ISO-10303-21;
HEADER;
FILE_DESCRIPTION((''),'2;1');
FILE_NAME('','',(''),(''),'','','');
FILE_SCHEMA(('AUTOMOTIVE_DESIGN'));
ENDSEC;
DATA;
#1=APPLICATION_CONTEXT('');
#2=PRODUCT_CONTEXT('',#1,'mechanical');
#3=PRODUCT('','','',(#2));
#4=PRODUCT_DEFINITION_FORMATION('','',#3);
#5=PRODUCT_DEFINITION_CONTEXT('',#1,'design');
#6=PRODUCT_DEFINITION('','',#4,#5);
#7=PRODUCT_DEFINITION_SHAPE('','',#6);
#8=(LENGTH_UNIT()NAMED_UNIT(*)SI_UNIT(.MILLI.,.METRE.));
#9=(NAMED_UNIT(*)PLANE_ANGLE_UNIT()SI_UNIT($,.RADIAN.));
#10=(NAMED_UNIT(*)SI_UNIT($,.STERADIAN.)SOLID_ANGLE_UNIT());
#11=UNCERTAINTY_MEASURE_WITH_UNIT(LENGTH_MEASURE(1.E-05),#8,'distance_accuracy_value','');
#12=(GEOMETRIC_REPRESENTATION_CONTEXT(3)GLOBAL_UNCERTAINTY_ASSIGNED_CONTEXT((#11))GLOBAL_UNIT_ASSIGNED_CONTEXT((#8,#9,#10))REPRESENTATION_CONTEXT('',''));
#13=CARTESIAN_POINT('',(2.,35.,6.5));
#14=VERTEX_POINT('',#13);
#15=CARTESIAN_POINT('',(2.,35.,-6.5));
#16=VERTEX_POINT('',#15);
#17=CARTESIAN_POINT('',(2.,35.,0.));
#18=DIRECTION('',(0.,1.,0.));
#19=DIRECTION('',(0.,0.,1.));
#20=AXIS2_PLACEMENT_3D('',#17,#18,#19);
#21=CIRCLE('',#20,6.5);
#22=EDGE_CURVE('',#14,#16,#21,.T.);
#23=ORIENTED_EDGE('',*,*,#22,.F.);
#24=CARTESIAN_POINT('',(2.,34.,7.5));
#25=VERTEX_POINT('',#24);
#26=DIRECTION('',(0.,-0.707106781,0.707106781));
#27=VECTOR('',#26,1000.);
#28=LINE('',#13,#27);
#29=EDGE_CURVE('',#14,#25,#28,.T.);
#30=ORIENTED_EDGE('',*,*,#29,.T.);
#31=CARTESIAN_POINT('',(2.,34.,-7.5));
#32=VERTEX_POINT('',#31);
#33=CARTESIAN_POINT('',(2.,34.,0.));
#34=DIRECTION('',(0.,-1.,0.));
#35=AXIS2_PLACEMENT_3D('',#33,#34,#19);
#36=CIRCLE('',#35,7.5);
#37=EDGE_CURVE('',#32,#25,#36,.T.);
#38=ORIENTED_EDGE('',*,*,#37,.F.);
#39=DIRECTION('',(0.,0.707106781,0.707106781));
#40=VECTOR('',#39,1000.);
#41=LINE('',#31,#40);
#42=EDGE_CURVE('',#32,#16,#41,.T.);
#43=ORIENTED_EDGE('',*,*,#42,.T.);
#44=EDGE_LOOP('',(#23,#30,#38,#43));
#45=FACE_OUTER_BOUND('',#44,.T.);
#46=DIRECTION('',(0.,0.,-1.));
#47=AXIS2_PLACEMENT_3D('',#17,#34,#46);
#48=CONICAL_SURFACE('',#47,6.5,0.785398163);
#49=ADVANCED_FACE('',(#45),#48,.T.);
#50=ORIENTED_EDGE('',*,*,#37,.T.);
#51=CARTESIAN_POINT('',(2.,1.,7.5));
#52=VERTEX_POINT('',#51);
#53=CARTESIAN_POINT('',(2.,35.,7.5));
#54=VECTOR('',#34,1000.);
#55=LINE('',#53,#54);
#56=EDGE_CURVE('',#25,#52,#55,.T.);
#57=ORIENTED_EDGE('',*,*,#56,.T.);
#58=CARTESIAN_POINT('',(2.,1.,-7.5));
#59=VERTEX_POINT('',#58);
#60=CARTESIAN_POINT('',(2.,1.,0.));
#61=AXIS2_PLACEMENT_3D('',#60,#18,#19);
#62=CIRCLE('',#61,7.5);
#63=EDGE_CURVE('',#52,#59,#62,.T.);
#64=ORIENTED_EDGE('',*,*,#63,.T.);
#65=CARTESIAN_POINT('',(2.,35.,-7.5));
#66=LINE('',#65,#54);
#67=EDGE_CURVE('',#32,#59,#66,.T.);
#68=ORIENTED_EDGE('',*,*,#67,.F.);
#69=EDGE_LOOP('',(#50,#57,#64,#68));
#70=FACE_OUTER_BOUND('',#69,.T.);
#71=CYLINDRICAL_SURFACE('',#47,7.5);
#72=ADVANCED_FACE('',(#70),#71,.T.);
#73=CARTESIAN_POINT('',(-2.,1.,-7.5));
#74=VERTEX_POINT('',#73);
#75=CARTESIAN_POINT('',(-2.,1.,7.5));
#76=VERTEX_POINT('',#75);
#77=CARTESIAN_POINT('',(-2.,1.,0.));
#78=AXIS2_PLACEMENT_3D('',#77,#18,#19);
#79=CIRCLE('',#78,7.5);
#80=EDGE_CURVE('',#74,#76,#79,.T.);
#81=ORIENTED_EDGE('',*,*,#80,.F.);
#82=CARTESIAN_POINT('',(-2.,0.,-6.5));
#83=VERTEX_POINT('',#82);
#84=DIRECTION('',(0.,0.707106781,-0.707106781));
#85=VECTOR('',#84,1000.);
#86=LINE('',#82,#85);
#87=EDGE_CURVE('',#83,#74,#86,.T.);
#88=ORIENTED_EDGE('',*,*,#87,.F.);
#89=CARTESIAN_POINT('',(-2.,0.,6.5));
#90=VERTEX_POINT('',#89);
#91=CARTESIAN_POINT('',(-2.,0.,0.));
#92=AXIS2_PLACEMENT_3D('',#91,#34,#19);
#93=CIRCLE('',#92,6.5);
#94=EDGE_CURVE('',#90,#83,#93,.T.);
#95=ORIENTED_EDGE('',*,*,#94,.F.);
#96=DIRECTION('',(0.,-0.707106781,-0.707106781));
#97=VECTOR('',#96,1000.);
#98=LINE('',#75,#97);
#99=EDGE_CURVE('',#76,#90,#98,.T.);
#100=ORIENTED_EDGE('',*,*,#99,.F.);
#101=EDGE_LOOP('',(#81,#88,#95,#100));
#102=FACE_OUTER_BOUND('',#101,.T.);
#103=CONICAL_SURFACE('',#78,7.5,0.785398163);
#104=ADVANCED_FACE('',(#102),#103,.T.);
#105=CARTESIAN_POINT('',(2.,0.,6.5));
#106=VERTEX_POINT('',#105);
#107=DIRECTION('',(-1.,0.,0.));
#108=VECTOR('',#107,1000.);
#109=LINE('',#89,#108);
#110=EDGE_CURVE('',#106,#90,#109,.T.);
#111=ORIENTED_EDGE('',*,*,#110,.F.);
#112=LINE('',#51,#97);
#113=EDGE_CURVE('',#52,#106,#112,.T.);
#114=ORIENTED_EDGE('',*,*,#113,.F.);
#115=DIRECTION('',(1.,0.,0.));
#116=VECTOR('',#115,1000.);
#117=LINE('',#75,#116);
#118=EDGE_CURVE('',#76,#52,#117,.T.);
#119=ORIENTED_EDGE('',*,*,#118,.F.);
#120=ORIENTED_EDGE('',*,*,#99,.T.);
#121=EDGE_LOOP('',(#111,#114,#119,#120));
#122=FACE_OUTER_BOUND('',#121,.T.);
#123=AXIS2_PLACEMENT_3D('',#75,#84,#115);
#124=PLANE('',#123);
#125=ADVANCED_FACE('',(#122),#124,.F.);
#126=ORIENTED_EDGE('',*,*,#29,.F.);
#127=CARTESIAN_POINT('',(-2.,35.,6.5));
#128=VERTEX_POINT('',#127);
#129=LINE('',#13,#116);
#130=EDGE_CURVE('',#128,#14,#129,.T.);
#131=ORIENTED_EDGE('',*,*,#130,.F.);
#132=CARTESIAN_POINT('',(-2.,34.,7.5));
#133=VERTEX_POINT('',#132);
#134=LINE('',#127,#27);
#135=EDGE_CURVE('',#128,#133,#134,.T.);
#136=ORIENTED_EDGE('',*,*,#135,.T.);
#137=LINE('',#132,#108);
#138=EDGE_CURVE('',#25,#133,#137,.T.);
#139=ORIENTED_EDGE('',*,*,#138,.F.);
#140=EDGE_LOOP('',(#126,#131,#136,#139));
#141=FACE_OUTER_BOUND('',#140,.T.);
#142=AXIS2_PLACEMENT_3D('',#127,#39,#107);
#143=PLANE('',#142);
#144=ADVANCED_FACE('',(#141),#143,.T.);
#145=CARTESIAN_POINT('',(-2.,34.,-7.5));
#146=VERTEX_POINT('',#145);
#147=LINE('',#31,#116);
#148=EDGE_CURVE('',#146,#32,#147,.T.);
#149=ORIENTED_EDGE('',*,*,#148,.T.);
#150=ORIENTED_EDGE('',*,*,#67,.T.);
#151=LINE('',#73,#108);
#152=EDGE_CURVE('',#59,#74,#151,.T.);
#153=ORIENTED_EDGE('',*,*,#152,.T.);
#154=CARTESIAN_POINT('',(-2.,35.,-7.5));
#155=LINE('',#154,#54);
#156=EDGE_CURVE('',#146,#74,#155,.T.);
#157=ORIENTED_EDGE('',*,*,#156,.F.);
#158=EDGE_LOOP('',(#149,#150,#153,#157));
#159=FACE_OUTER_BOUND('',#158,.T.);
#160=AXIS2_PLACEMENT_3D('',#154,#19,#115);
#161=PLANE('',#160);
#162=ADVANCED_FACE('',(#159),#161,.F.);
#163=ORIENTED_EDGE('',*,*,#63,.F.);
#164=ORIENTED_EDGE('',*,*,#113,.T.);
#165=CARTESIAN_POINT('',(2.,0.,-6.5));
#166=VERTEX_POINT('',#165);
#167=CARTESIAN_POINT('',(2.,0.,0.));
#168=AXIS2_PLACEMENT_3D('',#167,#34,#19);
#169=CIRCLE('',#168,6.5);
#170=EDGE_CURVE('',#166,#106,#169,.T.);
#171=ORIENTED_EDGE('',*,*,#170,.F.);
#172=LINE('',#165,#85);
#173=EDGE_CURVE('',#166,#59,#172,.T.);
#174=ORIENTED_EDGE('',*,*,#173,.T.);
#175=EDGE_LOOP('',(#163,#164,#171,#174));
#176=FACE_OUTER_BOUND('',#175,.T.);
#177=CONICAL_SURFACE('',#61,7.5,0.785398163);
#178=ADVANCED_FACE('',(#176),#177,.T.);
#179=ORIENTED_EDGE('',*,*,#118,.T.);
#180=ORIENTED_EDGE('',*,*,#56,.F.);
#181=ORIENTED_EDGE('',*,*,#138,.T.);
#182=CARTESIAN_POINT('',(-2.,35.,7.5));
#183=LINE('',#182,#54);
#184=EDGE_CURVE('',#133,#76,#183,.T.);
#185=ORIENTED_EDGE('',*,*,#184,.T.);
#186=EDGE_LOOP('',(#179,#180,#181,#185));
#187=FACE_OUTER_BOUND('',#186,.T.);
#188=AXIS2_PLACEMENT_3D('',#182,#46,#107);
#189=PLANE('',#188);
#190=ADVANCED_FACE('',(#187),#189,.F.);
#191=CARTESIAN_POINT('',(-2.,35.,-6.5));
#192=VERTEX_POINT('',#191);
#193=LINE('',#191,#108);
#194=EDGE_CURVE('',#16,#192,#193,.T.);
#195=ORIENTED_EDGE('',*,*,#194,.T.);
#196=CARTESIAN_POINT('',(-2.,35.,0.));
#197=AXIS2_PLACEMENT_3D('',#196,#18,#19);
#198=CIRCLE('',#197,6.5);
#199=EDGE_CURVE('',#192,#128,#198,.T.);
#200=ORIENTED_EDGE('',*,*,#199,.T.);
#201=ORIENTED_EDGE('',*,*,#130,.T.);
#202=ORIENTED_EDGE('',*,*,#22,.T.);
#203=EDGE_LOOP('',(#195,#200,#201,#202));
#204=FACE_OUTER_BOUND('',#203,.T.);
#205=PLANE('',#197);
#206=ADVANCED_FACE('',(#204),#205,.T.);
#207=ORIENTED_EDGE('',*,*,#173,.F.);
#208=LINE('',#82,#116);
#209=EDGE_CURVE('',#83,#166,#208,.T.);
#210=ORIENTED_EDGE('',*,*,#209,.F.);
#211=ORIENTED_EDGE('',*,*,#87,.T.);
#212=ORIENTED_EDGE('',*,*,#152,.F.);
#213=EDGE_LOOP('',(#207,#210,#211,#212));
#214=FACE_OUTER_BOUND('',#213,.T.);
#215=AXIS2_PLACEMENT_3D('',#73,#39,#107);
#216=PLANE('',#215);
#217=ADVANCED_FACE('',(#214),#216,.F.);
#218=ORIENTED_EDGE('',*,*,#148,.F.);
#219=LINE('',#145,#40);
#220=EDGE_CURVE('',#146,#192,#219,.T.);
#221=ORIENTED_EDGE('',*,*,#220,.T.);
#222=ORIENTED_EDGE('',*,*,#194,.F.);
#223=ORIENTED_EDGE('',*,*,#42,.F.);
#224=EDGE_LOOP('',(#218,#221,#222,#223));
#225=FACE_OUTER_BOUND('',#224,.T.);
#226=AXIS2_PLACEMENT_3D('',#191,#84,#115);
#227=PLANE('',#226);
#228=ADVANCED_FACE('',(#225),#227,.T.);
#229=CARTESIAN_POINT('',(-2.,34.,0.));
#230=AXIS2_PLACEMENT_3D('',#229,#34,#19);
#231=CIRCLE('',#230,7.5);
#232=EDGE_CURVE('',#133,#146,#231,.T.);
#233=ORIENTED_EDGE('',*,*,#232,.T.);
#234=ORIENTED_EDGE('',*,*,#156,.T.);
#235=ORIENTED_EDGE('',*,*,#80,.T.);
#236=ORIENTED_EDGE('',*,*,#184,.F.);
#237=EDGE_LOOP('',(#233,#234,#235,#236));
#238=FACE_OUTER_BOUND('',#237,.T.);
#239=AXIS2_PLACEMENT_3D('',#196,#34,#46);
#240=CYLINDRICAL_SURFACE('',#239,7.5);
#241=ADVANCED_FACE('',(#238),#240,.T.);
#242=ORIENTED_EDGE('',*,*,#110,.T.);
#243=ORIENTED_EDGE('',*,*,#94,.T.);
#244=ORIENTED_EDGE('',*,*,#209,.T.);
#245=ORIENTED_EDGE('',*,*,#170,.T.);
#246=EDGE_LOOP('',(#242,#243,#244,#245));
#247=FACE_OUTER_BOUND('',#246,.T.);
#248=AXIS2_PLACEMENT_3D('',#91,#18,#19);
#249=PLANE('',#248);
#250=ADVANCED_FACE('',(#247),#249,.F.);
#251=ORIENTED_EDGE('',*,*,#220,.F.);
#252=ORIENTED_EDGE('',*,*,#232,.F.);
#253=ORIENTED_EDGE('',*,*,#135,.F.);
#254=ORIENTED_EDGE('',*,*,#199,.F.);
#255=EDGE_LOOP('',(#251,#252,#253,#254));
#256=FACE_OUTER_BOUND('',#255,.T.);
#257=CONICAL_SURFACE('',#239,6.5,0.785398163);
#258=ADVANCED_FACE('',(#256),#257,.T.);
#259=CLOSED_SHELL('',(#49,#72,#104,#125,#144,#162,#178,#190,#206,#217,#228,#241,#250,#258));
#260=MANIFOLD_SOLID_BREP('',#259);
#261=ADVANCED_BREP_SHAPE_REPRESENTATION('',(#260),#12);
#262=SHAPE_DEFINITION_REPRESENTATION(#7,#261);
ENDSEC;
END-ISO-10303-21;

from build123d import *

# Parameters (mm, degrees)
BOSS_EXTRUDE1_DEPTH = 35
CHAMFER1_SIZE       = 1


with BuildPart() as part:
    # Sketch1 → Boss-Extrude1 (new body)
    with BuildSketch(Plane(origin=(0, 0, 0), x_dir=(1, 0, 0), z_dir=(0, 1, 0))):
        with BuildLine():
            Line((-2, 7.5), (2, 7.5))
            ThreePointArc((2, 7.5), (9.5, 0), (2, -7.5))
            Line((2, -7.5), (-2, -7.5))
            ThreePointArc((-2, -7.5), (-9.5, 0), (-2, 7.5))
        make_face()
    extrude(amount=BOSS_EXTRUDE1_DEPTH)

    # Chamfer1
    chamfer1_edges = [part.edges().sort_by_distance(p)[0] for p in [
        (9.5, 35, 0),
        (0, 35, -7.5),
        (-9.5, 35, 0),
        (0, 0, -7.5),
        (9.5, 0, 0),
        (0, 0, 7.5),
        (-9.5, 0, 0),
        (0, 35, 7.5),
    ]]
    chamfer(chamfer1_edges, length=CHAMFER1_SIZE)


solid = part.part
